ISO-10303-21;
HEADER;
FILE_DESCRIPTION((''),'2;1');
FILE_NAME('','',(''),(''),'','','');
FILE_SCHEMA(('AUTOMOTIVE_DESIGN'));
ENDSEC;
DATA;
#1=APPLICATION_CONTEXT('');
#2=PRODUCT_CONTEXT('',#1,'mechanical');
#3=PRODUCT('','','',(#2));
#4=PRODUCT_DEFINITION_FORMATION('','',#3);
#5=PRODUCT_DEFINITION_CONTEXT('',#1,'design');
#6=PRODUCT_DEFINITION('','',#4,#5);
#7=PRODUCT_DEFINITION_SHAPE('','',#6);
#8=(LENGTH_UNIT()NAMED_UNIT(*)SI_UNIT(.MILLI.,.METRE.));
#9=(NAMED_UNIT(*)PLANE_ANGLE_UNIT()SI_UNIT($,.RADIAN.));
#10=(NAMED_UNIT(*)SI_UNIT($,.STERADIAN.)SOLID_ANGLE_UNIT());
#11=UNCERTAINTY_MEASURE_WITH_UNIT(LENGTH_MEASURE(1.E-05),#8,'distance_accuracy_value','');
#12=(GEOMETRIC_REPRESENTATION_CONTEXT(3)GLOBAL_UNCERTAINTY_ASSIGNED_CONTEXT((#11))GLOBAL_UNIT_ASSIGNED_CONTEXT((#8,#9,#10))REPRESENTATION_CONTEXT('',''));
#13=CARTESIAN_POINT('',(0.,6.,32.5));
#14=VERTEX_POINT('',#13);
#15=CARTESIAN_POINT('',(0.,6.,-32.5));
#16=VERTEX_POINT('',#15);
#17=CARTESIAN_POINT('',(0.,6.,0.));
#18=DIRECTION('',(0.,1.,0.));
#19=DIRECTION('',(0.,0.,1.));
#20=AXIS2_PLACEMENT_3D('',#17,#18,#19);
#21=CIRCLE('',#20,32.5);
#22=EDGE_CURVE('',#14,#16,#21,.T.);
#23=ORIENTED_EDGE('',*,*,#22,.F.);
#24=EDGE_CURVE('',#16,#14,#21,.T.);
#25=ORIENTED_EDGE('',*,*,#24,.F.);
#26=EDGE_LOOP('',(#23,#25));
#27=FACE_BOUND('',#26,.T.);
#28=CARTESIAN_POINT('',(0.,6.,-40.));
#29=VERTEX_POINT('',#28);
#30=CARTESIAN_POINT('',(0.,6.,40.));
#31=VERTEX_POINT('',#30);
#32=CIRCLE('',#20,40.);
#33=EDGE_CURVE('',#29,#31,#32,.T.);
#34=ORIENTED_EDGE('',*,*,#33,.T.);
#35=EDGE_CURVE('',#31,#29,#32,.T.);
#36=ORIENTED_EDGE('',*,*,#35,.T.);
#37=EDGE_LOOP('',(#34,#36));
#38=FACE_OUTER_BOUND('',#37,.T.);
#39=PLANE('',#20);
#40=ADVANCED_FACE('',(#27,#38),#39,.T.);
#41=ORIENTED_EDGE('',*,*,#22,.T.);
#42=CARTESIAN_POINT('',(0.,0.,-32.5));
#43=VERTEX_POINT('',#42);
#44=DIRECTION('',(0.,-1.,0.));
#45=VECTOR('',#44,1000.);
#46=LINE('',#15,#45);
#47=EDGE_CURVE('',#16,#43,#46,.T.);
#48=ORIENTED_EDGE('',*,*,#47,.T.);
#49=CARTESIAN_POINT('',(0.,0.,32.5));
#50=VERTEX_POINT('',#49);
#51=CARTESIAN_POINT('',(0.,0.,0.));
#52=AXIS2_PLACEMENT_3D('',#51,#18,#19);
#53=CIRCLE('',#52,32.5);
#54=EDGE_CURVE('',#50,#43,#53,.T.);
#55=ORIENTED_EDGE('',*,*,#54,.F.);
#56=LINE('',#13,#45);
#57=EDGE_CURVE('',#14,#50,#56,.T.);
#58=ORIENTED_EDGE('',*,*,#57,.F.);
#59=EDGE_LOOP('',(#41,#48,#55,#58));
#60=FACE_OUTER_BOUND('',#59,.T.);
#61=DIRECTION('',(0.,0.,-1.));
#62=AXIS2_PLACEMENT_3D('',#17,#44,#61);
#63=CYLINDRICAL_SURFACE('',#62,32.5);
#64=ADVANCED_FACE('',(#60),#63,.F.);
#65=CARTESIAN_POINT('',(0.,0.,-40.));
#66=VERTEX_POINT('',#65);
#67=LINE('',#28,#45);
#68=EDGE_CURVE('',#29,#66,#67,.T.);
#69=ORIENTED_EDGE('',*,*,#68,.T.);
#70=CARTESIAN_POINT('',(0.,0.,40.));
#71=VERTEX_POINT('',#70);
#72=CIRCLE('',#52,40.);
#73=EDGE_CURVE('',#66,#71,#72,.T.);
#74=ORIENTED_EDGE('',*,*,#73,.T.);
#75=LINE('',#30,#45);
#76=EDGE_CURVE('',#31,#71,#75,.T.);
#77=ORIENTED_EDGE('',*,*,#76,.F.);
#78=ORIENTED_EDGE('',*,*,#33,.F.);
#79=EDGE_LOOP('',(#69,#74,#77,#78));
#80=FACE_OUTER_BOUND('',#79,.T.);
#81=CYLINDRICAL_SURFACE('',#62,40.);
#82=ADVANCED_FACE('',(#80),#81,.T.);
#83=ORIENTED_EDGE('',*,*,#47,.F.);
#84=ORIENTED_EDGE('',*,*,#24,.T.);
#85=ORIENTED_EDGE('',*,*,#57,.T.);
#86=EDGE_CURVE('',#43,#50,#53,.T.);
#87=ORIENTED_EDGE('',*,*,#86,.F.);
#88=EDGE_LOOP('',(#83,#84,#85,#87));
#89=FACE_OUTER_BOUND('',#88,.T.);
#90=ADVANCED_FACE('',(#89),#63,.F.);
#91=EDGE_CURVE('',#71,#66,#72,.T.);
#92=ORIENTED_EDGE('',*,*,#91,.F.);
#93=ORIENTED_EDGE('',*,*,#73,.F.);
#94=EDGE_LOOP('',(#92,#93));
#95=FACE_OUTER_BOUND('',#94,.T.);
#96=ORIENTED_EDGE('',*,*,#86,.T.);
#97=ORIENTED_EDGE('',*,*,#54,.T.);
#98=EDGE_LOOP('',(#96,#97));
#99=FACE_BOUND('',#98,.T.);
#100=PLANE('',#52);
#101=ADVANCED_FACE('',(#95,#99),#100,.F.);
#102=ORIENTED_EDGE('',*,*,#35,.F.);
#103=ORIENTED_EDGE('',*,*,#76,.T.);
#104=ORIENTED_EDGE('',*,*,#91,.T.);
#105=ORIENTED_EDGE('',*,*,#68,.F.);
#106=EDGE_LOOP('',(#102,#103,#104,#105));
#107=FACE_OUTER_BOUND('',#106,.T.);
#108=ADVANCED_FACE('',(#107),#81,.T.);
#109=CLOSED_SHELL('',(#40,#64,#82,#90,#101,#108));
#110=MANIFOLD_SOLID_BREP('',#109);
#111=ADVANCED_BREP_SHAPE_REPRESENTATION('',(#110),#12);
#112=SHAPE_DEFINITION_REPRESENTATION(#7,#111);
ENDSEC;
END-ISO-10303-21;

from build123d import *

# Parameters (mm, degrees)
SKETCH1_R           = 40
SKETCH1_R_2         = 32.5
BOSS_EXTRUDE1_DEPTH = 6


with BuildPart() as part:
    # Sketch1 → Boss-Extrude1 (new body)
    with BuildSketch(Plane(origin=(0, 0, 0), x_dir=(1, 0, 0), z_dir=(0, 1, 0))):
        with Locations(Location((0, 0, 0), (0, 0, 270))):
            Circle(SKETCH1_R)
        with Locations(Location((0, 0, 0), (0, 0, 270))):
            Circle(SKETCH1_R_2, mode=Mode.SUBTRACT)
    extrude(amount=BOSS_EXTRUDE1_DEPTH)


solid = part.part
